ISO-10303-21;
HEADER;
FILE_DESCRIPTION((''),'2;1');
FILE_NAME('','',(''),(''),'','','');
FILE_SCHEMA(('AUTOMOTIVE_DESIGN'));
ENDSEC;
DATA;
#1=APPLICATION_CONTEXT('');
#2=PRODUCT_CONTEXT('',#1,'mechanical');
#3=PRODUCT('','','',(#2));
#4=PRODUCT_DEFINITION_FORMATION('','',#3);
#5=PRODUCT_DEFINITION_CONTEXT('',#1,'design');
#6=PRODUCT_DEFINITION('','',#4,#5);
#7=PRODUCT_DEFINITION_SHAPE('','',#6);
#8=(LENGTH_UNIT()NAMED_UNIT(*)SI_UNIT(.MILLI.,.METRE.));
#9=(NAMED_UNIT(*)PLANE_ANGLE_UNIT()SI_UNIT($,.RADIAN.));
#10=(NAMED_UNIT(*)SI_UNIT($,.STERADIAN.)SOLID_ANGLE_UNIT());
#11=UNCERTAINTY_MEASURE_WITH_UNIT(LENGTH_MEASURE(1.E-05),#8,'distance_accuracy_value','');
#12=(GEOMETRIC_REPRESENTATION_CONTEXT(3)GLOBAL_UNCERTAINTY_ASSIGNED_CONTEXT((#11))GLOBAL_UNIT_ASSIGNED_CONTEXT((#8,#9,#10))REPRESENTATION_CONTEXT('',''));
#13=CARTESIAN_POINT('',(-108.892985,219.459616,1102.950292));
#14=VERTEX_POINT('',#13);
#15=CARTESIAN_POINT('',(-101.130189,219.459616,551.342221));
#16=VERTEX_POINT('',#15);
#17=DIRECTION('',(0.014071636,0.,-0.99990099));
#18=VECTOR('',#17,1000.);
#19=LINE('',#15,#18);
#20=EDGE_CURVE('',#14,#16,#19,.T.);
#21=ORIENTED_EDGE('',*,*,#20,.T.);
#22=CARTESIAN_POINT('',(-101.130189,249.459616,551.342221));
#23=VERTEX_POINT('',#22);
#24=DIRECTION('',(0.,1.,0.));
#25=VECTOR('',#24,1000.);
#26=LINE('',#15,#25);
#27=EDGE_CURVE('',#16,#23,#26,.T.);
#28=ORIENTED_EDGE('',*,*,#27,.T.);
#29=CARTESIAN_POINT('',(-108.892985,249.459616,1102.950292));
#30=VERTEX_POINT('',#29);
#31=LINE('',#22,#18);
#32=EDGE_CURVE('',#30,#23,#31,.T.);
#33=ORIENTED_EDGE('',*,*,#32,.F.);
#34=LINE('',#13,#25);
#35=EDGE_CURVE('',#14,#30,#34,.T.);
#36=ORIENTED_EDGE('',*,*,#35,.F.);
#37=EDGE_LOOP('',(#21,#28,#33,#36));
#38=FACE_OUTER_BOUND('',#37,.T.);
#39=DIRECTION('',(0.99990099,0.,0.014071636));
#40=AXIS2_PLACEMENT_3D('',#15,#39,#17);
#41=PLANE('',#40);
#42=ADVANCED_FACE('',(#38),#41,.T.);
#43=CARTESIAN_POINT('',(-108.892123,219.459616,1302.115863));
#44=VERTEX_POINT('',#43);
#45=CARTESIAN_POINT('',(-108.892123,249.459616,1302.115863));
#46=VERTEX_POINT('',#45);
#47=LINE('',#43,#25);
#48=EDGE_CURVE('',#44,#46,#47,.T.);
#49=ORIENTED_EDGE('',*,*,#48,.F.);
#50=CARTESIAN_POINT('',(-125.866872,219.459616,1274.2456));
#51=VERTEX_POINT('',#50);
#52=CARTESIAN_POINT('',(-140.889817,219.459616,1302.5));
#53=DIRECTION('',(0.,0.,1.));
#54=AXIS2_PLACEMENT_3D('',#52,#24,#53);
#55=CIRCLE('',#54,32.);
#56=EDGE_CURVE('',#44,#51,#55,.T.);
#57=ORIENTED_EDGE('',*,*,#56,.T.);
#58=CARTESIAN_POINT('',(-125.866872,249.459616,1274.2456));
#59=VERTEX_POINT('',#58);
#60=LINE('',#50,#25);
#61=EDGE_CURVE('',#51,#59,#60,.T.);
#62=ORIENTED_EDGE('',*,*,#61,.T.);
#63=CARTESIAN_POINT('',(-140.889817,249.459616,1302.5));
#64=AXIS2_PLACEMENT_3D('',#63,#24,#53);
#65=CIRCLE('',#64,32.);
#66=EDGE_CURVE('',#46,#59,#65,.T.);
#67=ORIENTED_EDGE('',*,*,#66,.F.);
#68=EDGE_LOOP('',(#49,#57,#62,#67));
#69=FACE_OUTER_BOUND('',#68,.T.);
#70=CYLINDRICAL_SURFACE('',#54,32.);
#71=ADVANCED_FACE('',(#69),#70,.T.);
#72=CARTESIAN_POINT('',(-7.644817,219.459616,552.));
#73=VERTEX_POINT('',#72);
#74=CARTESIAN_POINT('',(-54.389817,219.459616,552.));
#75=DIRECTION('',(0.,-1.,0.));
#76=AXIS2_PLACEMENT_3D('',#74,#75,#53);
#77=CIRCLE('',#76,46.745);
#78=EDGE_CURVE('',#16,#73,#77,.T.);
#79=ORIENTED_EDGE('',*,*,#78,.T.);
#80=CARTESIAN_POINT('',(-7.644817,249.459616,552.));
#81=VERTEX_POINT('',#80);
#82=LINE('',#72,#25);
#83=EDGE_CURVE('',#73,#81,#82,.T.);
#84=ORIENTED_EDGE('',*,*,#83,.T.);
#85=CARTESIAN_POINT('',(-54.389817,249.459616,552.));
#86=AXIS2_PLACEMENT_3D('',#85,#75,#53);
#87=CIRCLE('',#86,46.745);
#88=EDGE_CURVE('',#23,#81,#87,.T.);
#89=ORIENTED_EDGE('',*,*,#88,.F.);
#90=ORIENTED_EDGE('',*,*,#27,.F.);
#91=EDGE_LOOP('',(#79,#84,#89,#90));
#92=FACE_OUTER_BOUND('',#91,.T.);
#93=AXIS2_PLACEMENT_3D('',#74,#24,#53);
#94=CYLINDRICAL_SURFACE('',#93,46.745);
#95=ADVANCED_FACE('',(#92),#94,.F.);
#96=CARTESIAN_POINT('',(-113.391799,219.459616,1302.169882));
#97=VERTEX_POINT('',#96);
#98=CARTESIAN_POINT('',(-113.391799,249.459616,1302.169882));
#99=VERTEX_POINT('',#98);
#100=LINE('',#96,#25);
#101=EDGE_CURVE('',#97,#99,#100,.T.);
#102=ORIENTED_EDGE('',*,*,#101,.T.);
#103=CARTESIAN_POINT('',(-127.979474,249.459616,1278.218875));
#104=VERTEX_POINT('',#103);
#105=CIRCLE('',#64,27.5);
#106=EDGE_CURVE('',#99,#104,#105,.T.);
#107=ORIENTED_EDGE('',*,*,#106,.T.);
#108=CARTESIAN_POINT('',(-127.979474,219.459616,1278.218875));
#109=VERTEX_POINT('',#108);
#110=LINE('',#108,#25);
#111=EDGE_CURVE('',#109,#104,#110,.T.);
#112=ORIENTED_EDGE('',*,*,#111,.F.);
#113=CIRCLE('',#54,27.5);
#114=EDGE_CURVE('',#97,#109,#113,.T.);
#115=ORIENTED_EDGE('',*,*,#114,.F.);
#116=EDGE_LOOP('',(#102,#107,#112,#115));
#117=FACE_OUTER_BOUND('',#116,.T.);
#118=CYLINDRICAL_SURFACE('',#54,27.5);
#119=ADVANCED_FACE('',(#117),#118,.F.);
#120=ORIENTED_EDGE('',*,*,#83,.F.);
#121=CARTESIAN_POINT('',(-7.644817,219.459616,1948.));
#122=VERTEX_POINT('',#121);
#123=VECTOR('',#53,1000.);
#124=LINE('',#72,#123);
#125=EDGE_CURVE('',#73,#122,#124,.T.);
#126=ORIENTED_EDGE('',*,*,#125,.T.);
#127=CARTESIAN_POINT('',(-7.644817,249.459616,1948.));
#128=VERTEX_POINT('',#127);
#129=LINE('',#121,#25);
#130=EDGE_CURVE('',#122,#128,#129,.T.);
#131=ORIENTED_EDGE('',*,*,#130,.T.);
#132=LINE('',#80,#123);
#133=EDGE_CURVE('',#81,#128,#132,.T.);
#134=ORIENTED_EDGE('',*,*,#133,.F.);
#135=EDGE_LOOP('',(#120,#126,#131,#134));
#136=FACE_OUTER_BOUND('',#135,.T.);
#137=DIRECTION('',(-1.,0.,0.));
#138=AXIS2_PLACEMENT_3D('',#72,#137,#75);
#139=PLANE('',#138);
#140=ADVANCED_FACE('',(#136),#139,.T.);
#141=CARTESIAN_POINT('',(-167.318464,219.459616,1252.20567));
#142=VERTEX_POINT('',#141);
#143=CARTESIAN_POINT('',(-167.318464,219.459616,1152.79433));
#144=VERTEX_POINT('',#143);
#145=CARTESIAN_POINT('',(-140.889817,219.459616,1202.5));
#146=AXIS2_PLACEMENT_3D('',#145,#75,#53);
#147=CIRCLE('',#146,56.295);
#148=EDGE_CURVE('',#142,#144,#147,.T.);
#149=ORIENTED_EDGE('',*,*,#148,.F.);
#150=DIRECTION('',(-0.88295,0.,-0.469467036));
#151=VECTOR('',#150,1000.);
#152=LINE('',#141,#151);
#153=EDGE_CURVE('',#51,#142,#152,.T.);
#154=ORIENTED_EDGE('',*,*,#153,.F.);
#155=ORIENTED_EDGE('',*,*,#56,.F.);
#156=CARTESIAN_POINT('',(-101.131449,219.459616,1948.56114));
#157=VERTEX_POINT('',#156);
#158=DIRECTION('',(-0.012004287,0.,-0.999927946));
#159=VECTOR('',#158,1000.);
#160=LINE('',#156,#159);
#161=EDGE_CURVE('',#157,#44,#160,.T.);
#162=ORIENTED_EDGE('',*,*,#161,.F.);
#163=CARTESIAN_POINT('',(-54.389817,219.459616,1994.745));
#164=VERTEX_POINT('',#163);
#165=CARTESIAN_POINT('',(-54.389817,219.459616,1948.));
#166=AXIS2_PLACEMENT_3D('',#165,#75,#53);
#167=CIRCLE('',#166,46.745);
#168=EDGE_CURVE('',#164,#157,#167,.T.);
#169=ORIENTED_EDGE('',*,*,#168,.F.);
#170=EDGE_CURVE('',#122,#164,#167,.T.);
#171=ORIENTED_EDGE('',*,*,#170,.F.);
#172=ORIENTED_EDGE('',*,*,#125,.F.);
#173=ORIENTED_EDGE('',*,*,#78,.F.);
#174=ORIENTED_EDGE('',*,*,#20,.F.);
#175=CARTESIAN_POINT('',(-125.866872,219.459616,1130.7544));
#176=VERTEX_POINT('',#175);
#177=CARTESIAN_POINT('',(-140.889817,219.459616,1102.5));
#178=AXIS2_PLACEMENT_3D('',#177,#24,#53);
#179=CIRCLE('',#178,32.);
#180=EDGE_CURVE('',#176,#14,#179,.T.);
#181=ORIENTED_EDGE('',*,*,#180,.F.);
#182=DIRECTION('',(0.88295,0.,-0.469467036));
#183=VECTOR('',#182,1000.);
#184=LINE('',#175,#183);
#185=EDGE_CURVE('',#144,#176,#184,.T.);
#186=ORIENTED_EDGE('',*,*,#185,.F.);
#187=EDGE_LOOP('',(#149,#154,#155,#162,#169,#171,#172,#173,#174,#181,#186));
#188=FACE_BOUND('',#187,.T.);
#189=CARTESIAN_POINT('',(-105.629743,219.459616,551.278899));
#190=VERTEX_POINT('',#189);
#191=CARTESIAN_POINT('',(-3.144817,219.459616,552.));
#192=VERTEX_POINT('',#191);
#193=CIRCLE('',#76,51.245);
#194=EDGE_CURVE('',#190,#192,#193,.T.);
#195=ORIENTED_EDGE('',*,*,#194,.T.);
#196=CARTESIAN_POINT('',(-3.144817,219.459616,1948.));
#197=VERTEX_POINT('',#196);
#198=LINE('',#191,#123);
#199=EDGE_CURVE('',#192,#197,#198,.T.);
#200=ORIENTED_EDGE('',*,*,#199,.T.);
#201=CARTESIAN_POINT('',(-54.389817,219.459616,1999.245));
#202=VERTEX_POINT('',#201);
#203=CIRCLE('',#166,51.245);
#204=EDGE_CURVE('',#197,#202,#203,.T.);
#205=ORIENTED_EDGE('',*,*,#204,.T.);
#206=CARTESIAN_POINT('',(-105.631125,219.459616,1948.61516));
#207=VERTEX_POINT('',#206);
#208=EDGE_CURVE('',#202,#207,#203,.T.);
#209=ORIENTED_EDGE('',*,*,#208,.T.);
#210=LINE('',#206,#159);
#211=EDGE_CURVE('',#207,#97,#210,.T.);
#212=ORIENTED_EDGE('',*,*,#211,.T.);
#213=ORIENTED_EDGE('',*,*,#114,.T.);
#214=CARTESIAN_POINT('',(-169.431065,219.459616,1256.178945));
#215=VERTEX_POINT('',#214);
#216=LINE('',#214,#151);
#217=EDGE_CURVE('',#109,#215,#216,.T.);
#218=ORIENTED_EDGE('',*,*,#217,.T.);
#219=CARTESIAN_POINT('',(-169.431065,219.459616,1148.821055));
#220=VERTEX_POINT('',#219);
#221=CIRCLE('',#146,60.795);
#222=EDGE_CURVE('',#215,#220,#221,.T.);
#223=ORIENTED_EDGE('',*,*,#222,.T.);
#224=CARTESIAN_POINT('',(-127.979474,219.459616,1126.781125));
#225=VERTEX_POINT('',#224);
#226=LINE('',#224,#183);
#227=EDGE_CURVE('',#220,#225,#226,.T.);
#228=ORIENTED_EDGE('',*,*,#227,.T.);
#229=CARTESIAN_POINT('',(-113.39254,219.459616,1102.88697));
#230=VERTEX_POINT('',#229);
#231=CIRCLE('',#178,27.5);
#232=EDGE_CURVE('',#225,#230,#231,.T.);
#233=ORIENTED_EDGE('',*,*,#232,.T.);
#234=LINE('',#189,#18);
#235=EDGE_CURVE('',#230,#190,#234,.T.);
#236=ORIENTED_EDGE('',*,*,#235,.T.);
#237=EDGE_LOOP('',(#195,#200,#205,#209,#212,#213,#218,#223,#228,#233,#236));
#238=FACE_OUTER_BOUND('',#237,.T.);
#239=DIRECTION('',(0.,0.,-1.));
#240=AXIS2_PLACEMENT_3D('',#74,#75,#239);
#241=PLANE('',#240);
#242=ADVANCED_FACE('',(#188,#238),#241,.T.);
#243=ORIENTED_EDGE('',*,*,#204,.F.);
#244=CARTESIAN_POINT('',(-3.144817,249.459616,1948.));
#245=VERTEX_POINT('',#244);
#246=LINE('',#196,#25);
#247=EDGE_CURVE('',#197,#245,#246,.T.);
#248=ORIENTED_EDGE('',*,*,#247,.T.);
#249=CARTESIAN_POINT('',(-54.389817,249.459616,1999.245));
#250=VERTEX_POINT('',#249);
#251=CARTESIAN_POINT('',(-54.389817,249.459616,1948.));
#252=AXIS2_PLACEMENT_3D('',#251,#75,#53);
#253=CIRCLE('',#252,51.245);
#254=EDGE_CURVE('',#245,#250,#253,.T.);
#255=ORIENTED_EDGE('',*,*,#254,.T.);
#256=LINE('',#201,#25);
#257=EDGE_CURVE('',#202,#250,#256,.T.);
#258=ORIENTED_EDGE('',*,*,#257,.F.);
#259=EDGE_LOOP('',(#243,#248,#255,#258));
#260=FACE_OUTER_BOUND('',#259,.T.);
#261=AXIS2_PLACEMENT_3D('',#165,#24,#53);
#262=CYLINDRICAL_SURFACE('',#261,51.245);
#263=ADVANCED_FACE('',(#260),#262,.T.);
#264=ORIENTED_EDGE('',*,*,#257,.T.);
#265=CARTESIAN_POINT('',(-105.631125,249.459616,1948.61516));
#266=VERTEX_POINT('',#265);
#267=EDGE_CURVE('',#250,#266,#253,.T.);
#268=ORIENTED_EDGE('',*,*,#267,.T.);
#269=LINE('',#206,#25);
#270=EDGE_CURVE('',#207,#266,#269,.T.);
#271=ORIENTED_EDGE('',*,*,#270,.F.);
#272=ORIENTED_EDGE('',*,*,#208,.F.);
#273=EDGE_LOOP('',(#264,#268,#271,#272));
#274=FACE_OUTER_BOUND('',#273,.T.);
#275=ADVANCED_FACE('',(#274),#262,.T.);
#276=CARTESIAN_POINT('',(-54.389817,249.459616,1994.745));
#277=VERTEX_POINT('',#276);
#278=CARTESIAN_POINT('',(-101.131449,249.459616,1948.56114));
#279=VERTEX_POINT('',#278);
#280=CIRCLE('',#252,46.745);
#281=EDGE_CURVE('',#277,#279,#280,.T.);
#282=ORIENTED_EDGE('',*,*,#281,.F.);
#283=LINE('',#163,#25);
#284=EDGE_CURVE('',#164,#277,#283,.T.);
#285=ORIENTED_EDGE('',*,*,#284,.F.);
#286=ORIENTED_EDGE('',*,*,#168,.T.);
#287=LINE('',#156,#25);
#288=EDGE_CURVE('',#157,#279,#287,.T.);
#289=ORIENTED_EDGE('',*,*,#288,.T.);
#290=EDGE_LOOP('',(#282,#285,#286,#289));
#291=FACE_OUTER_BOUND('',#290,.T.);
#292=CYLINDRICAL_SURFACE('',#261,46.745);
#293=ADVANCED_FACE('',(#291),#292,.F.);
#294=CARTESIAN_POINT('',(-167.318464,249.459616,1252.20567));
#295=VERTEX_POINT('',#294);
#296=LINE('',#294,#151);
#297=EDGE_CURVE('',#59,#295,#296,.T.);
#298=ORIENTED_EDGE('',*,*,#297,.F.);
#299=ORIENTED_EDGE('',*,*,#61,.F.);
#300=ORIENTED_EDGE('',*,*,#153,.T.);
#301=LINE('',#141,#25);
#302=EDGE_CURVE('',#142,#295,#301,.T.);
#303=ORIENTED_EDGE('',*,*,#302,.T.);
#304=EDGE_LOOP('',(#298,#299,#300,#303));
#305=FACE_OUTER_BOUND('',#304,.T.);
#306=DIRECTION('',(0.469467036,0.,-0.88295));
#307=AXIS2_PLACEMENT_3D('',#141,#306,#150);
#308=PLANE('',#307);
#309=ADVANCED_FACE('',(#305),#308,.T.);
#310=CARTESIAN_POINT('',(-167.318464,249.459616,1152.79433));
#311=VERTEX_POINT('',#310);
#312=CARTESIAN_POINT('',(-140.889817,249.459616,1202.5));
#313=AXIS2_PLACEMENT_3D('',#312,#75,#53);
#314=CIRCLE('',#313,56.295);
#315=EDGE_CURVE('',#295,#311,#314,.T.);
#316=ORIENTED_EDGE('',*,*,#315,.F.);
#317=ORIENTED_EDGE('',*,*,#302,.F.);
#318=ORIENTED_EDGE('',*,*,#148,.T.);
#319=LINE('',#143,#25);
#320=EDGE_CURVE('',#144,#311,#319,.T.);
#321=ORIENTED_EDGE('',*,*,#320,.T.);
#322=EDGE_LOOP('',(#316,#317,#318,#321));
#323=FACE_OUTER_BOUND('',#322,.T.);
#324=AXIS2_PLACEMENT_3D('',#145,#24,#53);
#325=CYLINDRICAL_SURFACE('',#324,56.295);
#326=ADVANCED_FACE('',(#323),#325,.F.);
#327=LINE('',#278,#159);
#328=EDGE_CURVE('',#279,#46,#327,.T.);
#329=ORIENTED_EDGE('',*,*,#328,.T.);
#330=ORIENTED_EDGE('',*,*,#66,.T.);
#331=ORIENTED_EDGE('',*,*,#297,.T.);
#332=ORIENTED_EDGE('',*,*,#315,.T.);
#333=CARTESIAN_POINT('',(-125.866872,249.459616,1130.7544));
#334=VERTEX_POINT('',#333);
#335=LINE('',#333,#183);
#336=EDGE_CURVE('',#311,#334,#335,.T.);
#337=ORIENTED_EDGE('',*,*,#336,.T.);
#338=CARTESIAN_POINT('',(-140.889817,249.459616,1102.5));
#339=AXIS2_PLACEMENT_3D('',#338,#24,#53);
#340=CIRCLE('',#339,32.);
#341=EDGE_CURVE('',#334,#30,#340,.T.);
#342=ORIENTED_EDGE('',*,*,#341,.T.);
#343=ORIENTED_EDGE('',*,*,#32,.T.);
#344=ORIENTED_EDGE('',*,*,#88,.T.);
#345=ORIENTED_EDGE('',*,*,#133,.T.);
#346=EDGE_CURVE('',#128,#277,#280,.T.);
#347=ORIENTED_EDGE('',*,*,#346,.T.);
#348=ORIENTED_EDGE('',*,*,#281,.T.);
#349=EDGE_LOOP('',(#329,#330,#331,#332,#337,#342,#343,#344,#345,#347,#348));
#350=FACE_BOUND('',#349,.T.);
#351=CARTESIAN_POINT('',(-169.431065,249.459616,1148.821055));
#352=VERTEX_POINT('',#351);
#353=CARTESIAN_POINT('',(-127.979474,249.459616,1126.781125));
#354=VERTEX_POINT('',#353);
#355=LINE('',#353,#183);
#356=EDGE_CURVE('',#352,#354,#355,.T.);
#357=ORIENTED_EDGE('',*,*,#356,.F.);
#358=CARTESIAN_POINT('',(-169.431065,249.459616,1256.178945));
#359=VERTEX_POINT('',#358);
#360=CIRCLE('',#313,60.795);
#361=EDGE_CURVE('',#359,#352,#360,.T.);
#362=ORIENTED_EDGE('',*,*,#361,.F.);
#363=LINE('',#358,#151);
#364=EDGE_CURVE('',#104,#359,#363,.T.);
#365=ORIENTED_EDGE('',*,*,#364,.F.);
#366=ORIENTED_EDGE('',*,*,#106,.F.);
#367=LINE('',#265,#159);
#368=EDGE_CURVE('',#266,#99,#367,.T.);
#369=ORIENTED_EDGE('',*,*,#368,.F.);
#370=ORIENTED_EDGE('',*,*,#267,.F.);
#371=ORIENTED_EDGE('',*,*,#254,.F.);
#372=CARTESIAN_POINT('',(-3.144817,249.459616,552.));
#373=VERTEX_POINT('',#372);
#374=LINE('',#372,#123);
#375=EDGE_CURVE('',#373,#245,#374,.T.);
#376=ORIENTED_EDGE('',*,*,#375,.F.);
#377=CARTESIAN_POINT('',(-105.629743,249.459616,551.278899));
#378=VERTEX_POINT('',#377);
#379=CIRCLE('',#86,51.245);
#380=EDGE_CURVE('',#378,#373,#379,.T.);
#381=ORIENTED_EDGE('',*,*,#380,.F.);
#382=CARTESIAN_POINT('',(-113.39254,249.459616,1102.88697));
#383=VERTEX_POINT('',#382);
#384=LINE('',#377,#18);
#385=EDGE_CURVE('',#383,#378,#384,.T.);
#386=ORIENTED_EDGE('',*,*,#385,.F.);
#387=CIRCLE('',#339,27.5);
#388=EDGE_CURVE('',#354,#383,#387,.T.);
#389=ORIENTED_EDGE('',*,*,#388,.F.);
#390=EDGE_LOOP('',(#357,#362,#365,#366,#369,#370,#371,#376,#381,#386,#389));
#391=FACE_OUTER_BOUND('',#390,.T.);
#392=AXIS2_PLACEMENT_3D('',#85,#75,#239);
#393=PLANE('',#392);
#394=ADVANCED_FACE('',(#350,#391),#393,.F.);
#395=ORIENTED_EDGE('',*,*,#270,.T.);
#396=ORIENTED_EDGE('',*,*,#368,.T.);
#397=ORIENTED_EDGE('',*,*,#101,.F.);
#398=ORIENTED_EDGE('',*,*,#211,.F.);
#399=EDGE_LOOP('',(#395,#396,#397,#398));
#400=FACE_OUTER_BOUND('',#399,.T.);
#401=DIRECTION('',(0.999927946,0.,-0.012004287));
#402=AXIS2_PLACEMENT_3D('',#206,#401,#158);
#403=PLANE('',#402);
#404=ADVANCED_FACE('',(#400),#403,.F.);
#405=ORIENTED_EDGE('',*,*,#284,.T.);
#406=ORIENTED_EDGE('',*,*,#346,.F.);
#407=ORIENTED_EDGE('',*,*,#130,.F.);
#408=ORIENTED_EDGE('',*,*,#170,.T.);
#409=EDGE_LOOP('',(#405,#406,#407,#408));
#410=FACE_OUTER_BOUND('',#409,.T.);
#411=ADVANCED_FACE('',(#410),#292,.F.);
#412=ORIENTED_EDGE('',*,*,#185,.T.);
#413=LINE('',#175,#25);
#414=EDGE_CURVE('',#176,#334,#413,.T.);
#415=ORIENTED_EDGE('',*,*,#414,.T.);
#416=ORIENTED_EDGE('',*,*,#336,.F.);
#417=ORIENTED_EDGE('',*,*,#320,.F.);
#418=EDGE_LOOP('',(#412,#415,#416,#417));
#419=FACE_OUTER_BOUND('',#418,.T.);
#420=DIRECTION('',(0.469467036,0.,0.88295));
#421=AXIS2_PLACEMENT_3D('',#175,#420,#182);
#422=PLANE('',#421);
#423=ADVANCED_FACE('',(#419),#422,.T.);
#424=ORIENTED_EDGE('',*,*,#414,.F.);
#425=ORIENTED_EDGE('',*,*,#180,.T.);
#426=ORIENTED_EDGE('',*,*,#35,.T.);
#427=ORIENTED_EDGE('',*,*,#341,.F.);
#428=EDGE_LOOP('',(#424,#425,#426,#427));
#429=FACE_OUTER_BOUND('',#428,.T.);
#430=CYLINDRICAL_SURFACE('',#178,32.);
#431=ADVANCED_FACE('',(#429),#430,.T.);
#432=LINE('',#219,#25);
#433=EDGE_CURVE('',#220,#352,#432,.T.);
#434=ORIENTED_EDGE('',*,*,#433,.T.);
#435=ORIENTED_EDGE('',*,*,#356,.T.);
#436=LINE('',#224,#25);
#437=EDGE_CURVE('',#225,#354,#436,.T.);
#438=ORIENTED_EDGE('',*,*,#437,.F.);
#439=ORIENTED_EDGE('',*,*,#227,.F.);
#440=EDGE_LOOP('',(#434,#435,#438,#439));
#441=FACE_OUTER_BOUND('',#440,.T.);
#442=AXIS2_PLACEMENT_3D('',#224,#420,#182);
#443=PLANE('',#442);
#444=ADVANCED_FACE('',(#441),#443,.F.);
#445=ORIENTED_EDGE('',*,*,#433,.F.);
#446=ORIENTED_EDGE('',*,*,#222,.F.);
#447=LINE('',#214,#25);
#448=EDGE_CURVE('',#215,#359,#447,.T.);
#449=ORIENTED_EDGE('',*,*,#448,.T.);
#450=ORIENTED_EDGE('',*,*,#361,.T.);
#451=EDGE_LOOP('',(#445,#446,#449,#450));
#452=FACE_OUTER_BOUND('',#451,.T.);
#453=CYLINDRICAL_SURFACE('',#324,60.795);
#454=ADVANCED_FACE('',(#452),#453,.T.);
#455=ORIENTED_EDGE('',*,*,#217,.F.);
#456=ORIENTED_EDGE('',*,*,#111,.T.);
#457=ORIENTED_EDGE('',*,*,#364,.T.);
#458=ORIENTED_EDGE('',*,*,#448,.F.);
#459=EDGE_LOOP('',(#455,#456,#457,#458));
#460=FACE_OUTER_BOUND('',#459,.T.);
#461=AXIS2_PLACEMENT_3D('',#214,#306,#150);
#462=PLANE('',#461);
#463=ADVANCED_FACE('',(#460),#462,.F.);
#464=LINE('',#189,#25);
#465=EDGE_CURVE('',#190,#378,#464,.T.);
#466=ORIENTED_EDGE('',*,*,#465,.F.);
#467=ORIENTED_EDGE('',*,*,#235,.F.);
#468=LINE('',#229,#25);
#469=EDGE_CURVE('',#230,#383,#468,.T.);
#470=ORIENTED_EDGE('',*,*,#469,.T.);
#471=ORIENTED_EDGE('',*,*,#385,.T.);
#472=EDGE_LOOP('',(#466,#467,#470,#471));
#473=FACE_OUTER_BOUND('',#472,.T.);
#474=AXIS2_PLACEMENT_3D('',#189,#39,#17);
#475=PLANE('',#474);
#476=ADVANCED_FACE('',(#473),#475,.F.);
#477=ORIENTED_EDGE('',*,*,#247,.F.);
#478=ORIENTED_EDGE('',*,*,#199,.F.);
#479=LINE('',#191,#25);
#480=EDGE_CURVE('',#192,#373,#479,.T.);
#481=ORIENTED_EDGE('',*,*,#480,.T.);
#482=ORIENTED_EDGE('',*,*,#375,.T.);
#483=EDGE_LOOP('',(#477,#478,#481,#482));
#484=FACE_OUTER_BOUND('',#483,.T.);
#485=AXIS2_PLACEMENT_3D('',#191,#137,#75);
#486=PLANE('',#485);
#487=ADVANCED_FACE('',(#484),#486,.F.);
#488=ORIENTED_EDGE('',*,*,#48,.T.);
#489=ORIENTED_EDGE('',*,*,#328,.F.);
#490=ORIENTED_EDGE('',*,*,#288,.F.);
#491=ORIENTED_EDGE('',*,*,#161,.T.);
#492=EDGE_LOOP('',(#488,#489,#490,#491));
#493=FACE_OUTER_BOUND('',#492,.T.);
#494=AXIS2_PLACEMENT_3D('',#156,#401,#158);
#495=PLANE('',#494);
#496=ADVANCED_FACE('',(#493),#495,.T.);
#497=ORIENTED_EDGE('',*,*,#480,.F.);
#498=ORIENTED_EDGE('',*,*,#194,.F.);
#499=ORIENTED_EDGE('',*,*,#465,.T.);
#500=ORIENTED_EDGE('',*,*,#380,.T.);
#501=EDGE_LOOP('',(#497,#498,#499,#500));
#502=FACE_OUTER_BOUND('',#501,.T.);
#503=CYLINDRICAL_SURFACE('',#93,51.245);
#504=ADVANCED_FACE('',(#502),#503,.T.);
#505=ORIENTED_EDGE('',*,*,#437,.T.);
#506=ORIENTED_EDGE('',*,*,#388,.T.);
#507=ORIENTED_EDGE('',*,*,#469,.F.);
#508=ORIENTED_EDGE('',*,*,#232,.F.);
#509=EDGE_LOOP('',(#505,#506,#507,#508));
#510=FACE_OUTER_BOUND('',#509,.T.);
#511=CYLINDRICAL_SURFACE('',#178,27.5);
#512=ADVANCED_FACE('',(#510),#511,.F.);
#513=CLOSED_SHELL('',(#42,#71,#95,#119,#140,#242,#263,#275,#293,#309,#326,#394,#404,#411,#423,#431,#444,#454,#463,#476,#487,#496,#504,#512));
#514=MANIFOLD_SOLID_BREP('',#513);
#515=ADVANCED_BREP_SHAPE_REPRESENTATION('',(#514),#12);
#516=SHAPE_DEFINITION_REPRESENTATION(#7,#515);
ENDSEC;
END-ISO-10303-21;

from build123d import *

# Parameters (mm, degrees)
EXTRUDE_1_DEPTH = 15


with BuildPart() as part:
    # 草图1 → 拉伸-薄壁1 (new, symmetric)
    with BuildSketch(Plane(origin=(-54.389817032, 234.459616021, 1948), x_dir=(0, 0, 1), z_dir=(0, -1, 0))):
        with BuildLine():
            Line((-669.781125, 73.589656521), (-691.82105475, 115.041248428))
            ThreePointArc((-691.82105475, 115.041248428), (-745.5, 147.295), (-799.17894525, 115.041248428))
            Line((-799.17894525, 115.041248428), (-821.218875, 73.589656521))
            ThreePointArc((-821.218875, 73.589656521), (-831.170890239, 63.02817405), (-845.113030011, 59.002722785))
            Line((-845.113030011, 59.002722785), (-1396.721100985, 51.239926214))
            ThreePointArc((-1396.721100985, 51.239926214), (-1447.243731538, -0.360559418), (-1396, -51.245))
            Line((-1396, -51.245), (0, -51.245))
            ThreePointArc((0, -51.245), (51.244076889, -0.307585387), (0.615159693, 51.24130759))
            Line((0.615159693, 51.24130759), (-645.830117895, 59.001981486))
            ThreePointArc((-645.830117895, 59.001981486), (-659.804837816, 63.013373698), (-669.781125, 73.589656521))
        make_face()
        with BuildLine():
            Line((-673.7544, 71.477054861), (-695.79432975, 112.928646768))
            ThreePointArc((-695.79432975, 112.928646768), (-745.5, 142.795), (-795.20567025, 112.928646768))
            Line((-795.20567025, 112.928646768), (-817.2456, 71.477054861))
            ThreePointArc((-817.2456, 71.477054861), (-828.826126823, 59.187329803), (-845.049707649, 54.503168332))
            Line((-845.049707649, 54.503168332), (-1396.657778624, 46.74037176))
            ThreePointArc((-1396.657778624, 46.74037176), (-1442.743842926, -0.328897453), (-1396, -46.745))
            Line((-1396, -46.745), (0, -46.745))
            ThreePointArc((0, -46.745), (46.744157951, -0.280575254), (0.561140401, 46.741631833))
            Line((0.561140401, 46.741631833), (-645.884137187, 54.50230573))
            ThreePointArc((-645.884137187, 54.50230573), (-662.145629459, 59.170107576), (-673.7544, 71.477054861))
        make_face(mode=Mode.SUBTRACT)
    extrude(amount=EXTRUDE_1_DEPTH, both=True)


solid = part.part
